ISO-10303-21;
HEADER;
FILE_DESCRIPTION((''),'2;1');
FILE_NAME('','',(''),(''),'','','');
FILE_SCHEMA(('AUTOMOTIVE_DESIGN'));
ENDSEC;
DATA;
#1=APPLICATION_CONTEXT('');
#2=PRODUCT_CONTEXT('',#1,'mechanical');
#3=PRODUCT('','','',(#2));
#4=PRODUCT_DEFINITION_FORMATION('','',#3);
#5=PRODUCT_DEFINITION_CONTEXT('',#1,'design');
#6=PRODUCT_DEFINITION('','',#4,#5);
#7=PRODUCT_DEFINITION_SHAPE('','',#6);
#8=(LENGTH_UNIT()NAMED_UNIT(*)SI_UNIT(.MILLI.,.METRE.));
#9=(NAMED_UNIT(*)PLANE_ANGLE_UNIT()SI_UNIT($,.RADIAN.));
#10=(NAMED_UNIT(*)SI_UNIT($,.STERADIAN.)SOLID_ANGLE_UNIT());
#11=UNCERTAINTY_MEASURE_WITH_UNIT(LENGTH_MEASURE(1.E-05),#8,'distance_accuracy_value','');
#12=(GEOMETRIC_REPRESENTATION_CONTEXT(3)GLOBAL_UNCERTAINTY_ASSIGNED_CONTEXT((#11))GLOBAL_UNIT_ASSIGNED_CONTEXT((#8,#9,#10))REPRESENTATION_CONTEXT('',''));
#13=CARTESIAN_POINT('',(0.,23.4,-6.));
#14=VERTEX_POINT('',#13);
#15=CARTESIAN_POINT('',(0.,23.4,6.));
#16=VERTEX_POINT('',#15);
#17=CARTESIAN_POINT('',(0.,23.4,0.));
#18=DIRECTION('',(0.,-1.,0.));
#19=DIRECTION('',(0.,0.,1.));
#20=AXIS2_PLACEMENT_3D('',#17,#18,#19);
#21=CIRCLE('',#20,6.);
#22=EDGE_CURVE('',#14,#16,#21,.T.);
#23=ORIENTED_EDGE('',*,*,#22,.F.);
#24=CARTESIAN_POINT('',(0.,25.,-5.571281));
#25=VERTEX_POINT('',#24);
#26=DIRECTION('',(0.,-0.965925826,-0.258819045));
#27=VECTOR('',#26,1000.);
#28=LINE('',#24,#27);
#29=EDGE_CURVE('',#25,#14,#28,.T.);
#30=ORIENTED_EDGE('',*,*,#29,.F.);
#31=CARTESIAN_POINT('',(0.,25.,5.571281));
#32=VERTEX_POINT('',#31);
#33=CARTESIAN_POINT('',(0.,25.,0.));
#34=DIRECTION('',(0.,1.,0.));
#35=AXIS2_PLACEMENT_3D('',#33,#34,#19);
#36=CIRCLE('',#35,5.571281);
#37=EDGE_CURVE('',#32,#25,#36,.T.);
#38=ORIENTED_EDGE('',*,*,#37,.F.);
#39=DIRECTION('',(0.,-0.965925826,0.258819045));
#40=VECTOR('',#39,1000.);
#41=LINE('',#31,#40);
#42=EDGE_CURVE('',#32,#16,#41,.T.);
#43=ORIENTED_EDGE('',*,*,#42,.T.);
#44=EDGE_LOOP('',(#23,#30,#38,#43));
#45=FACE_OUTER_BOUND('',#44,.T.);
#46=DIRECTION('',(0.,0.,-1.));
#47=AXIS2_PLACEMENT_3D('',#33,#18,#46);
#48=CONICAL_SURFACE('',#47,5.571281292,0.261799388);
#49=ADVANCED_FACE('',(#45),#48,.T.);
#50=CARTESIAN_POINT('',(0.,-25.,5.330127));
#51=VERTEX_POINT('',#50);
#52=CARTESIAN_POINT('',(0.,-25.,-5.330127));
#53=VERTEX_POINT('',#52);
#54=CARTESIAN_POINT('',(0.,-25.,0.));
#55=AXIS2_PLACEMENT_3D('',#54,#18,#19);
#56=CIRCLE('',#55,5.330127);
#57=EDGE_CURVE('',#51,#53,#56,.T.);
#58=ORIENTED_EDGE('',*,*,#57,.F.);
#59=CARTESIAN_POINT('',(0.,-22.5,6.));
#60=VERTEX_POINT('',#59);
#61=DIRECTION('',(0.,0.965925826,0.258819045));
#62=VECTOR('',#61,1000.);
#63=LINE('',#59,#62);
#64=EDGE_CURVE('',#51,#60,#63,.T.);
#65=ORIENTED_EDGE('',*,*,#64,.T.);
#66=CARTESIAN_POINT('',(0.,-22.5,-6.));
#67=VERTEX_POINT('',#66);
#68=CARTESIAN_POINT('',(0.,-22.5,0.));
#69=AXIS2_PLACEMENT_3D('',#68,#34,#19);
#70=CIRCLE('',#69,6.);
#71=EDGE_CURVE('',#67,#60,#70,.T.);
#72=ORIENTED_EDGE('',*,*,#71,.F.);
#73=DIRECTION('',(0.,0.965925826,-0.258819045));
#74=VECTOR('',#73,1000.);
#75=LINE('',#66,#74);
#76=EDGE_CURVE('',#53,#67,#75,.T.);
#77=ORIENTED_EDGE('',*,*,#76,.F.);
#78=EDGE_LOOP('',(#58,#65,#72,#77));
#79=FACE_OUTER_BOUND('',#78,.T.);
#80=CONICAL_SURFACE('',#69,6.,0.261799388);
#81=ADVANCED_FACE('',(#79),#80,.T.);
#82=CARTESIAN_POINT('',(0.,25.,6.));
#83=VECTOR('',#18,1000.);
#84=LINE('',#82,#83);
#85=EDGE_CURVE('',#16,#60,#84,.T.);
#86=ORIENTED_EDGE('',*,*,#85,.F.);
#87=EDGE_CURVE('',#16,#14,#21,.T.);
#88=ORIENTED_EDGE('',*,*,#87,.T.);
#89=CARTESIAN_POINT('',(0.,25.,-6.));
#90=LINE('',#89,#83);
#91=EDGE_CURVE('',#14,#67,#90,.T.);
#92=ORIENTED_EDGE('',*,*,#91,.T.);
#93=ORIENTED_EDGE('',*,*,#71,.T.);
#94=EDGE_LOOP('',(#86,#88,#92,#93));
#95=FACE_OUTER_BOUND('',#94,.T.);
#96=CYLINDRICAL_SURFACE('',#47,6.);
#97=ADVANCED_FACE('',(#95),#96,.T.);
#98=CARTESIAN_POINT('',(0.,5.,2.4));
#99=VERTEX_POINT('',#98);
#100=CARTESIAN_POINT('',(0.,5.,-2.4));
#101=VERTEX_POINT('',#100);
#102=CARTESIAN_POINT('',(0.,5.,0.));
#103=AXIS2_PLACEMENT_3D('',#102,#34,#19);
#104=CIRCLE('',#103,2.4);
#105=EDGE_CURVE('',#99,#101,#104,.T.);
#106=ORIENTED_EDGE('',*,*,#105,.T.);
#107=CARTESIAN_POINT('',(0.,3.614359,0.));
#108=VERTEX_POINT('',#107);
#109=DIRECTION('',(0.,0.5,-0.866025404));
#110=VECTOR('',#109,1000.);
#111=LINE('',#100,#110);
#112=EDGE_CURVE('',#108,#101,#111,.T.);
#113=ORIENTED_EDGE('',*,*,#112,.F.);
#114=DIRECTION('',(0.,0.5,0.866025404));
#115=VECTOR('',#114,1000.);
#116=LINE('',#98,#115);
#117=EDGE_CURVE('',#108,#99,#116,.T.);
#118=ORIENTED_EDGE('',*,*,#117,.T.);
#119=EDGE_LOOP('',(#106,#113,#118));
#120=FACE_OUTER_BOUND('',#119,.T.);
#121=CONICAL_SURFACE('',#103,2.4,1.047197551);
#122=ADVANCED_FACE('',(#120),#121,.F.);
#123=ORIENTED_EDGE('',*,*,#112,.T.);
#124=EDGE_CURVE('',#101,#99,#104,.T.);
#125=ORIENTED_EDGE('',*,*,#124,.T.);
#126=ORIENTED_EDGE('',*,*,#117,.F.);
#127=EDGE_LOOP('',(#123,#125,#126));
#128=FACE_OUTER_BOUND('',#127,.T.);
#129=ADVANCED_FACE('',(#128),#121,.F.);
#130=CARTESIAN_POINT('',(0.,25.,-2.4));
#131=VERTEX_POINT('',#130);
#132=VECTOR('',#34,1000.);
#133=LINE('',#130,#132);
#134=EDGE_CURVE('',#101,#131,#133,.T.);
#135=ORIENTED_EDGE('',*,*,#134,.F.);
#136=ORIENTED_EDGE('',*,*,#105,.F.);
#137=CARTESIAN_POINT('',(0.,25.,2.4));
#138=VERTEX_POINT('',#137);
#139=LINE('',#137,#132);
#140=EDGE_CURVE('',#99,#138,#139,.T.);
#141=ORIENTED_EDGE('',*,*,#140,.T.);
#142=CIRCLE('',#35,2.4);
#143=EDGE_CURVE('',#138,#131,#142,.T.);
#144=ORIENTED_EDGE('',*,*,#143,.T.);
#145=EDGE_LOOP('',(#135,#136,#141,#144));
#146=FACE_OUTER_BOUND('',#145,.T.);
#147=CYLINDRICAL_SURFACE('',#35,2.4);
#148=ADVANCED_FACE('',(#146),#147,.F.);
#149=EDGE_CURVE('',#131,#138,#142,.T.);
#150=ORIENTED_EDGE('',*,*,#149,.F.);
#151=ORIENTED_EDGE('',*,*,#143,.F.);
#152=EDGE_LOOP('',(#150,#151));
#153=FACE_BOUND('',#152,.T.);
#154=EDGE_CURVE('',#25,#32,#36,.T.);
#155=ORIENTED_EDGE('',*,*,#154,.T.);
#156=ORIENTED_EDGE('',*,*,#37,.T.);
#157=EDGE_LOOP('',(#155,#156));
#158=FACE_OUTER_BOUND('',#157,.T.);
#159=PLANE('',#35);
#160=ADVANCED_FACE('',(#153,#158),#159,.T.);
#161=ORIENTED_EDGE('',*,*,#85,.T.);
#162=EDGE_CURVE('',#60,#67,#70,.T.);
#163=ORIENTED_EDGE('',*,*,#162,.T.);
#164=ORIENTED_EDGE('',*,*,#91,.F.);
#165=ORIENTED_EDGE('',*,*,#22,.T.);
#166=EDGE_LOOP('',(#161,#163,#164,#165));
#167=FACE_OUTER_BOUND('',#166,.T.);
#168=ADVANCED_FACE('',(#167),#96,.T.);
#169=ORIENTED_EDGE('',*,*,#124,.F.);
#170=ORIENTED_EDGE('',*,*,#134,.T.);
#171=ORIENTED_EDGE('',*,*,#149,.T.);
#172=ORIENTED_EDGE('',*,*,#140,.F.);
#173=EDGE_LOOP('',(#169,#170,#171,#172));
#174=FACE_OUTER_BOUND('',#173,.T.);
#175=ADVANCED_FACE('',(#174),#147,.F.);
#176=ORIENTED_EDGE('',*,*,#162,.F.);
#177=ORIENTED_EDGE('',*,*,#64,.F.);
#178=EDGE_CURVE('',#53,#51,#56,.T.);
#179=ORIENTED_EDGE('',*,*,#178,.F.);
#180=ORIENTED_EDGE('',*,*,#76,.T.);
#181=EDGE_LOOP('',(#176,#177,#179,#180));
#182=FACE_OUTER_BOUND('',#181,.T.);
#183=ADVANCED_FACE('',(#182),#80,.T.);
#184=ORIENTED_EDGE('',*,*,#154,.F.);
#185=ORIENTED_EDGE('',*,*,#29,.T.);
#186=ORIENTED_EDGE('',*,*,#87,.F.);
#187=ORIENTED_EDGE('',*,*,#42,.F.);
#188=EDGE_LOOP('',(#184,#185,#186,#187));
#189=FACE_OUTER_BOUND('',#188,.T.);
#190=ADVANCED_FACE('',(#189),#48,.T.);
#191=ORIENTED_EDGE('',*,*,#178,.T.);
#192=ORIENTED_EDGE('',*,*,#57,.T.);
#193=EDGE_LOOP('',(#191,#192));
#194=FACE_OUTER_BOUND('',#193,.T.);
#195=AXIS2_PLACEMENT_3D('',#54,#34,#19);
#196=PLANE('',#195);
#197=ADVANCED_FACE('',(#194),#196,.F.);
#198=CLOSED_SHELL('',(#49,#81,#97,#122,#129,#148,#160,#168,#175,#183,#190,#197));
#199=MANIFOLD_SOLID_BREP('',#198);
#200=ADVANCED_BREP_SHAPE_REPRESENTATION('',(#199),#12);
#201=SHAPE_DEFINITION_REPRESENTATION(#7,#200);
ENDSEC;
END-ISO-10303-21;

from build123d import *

# Parameters (mm, degrees)
SKETCH1_R             = 6
BOSS_EXTRUDE1_DEPTH   = 25
M6_TAPPED_HOLE1_D     = 4.8
M6_TAPPED_HOLE1_DEPTH = 20
M6_TAPPED_HOLE1_TIP   = 1.385640646
CHAMFER1_SIZE         = 1.6
CHAMFER1_SIZE2        = 0.428718708
CHAMFER2_SIZE         = 2.5
CHAMFER2_SIZE2        = 0.669872981


with BuildPart() as part:
    # Sketch1 → Boss-Extrude1 (new, symmetric)
    with BuildSketch(Plane(origin=(0, 0, 0), x_dir=(1, 0, 0), z_dir=(0, 1, 0))):
        with Locations(Location((0, 0, 0), (0, 0, 270))):
            Circle(SKETCH1_R)
    extrude(amount=BOSS_EXTRUDE1_DEPTH, both=True)

    # M6 Tapped Hole1
    with Locations(Plane(origin=(0, 25, 0), x_dir=(1, 0, 0), z_dir=(0, 1, 0))):
        with Locations((0, 0)):
            Hole(M6_TAPPED_HOLE1_D / 2, depth=M6_TAPPED_HOLE1_DEPTH)
            with Locations((0, 0, -(M6_TAPPED_HOLE1_DEPTH + M6_TAPPED_HOLE1_TIP / 2))):  # 120° drill point
                Cone(0, M6_TAPPED_HOLE1_D / 2, M6_TAPPED_HOLE1_TIP, mode=Mode.SUBTRACT)

    # Chamfer1
    chamfer1_edges = [part.edges().sort_by_distance(p)[0] for p in [
        (0, 25, -6),
    ]]
    chamfer1_side = [part.faces().sort_by_distance(p)[0] for p in [
        (0, 0, -6),
    ]]
    chamfer(chamfer1_edges, length=CHAMFER1_SIZE, length2=CHAMFER1_SIZE2, reference=chamfer1_side[0])

    # Chamfer2
    chamfer2_edges = [part.edges().sort_by_distance(p)[0] for p in [
        (0, -25, -6),
    ]]
    chamfer2_side = [part.faces().sort_by_distance(p)[0] for p in [
        (0, -0.8, -6),
    ]]
    chamfer(chamfer2_edges, length=CHAMFER2_SIZE, length2=CHAMFER2_SIZE2, reference=chamfer2_side[0])


solid = part.part
